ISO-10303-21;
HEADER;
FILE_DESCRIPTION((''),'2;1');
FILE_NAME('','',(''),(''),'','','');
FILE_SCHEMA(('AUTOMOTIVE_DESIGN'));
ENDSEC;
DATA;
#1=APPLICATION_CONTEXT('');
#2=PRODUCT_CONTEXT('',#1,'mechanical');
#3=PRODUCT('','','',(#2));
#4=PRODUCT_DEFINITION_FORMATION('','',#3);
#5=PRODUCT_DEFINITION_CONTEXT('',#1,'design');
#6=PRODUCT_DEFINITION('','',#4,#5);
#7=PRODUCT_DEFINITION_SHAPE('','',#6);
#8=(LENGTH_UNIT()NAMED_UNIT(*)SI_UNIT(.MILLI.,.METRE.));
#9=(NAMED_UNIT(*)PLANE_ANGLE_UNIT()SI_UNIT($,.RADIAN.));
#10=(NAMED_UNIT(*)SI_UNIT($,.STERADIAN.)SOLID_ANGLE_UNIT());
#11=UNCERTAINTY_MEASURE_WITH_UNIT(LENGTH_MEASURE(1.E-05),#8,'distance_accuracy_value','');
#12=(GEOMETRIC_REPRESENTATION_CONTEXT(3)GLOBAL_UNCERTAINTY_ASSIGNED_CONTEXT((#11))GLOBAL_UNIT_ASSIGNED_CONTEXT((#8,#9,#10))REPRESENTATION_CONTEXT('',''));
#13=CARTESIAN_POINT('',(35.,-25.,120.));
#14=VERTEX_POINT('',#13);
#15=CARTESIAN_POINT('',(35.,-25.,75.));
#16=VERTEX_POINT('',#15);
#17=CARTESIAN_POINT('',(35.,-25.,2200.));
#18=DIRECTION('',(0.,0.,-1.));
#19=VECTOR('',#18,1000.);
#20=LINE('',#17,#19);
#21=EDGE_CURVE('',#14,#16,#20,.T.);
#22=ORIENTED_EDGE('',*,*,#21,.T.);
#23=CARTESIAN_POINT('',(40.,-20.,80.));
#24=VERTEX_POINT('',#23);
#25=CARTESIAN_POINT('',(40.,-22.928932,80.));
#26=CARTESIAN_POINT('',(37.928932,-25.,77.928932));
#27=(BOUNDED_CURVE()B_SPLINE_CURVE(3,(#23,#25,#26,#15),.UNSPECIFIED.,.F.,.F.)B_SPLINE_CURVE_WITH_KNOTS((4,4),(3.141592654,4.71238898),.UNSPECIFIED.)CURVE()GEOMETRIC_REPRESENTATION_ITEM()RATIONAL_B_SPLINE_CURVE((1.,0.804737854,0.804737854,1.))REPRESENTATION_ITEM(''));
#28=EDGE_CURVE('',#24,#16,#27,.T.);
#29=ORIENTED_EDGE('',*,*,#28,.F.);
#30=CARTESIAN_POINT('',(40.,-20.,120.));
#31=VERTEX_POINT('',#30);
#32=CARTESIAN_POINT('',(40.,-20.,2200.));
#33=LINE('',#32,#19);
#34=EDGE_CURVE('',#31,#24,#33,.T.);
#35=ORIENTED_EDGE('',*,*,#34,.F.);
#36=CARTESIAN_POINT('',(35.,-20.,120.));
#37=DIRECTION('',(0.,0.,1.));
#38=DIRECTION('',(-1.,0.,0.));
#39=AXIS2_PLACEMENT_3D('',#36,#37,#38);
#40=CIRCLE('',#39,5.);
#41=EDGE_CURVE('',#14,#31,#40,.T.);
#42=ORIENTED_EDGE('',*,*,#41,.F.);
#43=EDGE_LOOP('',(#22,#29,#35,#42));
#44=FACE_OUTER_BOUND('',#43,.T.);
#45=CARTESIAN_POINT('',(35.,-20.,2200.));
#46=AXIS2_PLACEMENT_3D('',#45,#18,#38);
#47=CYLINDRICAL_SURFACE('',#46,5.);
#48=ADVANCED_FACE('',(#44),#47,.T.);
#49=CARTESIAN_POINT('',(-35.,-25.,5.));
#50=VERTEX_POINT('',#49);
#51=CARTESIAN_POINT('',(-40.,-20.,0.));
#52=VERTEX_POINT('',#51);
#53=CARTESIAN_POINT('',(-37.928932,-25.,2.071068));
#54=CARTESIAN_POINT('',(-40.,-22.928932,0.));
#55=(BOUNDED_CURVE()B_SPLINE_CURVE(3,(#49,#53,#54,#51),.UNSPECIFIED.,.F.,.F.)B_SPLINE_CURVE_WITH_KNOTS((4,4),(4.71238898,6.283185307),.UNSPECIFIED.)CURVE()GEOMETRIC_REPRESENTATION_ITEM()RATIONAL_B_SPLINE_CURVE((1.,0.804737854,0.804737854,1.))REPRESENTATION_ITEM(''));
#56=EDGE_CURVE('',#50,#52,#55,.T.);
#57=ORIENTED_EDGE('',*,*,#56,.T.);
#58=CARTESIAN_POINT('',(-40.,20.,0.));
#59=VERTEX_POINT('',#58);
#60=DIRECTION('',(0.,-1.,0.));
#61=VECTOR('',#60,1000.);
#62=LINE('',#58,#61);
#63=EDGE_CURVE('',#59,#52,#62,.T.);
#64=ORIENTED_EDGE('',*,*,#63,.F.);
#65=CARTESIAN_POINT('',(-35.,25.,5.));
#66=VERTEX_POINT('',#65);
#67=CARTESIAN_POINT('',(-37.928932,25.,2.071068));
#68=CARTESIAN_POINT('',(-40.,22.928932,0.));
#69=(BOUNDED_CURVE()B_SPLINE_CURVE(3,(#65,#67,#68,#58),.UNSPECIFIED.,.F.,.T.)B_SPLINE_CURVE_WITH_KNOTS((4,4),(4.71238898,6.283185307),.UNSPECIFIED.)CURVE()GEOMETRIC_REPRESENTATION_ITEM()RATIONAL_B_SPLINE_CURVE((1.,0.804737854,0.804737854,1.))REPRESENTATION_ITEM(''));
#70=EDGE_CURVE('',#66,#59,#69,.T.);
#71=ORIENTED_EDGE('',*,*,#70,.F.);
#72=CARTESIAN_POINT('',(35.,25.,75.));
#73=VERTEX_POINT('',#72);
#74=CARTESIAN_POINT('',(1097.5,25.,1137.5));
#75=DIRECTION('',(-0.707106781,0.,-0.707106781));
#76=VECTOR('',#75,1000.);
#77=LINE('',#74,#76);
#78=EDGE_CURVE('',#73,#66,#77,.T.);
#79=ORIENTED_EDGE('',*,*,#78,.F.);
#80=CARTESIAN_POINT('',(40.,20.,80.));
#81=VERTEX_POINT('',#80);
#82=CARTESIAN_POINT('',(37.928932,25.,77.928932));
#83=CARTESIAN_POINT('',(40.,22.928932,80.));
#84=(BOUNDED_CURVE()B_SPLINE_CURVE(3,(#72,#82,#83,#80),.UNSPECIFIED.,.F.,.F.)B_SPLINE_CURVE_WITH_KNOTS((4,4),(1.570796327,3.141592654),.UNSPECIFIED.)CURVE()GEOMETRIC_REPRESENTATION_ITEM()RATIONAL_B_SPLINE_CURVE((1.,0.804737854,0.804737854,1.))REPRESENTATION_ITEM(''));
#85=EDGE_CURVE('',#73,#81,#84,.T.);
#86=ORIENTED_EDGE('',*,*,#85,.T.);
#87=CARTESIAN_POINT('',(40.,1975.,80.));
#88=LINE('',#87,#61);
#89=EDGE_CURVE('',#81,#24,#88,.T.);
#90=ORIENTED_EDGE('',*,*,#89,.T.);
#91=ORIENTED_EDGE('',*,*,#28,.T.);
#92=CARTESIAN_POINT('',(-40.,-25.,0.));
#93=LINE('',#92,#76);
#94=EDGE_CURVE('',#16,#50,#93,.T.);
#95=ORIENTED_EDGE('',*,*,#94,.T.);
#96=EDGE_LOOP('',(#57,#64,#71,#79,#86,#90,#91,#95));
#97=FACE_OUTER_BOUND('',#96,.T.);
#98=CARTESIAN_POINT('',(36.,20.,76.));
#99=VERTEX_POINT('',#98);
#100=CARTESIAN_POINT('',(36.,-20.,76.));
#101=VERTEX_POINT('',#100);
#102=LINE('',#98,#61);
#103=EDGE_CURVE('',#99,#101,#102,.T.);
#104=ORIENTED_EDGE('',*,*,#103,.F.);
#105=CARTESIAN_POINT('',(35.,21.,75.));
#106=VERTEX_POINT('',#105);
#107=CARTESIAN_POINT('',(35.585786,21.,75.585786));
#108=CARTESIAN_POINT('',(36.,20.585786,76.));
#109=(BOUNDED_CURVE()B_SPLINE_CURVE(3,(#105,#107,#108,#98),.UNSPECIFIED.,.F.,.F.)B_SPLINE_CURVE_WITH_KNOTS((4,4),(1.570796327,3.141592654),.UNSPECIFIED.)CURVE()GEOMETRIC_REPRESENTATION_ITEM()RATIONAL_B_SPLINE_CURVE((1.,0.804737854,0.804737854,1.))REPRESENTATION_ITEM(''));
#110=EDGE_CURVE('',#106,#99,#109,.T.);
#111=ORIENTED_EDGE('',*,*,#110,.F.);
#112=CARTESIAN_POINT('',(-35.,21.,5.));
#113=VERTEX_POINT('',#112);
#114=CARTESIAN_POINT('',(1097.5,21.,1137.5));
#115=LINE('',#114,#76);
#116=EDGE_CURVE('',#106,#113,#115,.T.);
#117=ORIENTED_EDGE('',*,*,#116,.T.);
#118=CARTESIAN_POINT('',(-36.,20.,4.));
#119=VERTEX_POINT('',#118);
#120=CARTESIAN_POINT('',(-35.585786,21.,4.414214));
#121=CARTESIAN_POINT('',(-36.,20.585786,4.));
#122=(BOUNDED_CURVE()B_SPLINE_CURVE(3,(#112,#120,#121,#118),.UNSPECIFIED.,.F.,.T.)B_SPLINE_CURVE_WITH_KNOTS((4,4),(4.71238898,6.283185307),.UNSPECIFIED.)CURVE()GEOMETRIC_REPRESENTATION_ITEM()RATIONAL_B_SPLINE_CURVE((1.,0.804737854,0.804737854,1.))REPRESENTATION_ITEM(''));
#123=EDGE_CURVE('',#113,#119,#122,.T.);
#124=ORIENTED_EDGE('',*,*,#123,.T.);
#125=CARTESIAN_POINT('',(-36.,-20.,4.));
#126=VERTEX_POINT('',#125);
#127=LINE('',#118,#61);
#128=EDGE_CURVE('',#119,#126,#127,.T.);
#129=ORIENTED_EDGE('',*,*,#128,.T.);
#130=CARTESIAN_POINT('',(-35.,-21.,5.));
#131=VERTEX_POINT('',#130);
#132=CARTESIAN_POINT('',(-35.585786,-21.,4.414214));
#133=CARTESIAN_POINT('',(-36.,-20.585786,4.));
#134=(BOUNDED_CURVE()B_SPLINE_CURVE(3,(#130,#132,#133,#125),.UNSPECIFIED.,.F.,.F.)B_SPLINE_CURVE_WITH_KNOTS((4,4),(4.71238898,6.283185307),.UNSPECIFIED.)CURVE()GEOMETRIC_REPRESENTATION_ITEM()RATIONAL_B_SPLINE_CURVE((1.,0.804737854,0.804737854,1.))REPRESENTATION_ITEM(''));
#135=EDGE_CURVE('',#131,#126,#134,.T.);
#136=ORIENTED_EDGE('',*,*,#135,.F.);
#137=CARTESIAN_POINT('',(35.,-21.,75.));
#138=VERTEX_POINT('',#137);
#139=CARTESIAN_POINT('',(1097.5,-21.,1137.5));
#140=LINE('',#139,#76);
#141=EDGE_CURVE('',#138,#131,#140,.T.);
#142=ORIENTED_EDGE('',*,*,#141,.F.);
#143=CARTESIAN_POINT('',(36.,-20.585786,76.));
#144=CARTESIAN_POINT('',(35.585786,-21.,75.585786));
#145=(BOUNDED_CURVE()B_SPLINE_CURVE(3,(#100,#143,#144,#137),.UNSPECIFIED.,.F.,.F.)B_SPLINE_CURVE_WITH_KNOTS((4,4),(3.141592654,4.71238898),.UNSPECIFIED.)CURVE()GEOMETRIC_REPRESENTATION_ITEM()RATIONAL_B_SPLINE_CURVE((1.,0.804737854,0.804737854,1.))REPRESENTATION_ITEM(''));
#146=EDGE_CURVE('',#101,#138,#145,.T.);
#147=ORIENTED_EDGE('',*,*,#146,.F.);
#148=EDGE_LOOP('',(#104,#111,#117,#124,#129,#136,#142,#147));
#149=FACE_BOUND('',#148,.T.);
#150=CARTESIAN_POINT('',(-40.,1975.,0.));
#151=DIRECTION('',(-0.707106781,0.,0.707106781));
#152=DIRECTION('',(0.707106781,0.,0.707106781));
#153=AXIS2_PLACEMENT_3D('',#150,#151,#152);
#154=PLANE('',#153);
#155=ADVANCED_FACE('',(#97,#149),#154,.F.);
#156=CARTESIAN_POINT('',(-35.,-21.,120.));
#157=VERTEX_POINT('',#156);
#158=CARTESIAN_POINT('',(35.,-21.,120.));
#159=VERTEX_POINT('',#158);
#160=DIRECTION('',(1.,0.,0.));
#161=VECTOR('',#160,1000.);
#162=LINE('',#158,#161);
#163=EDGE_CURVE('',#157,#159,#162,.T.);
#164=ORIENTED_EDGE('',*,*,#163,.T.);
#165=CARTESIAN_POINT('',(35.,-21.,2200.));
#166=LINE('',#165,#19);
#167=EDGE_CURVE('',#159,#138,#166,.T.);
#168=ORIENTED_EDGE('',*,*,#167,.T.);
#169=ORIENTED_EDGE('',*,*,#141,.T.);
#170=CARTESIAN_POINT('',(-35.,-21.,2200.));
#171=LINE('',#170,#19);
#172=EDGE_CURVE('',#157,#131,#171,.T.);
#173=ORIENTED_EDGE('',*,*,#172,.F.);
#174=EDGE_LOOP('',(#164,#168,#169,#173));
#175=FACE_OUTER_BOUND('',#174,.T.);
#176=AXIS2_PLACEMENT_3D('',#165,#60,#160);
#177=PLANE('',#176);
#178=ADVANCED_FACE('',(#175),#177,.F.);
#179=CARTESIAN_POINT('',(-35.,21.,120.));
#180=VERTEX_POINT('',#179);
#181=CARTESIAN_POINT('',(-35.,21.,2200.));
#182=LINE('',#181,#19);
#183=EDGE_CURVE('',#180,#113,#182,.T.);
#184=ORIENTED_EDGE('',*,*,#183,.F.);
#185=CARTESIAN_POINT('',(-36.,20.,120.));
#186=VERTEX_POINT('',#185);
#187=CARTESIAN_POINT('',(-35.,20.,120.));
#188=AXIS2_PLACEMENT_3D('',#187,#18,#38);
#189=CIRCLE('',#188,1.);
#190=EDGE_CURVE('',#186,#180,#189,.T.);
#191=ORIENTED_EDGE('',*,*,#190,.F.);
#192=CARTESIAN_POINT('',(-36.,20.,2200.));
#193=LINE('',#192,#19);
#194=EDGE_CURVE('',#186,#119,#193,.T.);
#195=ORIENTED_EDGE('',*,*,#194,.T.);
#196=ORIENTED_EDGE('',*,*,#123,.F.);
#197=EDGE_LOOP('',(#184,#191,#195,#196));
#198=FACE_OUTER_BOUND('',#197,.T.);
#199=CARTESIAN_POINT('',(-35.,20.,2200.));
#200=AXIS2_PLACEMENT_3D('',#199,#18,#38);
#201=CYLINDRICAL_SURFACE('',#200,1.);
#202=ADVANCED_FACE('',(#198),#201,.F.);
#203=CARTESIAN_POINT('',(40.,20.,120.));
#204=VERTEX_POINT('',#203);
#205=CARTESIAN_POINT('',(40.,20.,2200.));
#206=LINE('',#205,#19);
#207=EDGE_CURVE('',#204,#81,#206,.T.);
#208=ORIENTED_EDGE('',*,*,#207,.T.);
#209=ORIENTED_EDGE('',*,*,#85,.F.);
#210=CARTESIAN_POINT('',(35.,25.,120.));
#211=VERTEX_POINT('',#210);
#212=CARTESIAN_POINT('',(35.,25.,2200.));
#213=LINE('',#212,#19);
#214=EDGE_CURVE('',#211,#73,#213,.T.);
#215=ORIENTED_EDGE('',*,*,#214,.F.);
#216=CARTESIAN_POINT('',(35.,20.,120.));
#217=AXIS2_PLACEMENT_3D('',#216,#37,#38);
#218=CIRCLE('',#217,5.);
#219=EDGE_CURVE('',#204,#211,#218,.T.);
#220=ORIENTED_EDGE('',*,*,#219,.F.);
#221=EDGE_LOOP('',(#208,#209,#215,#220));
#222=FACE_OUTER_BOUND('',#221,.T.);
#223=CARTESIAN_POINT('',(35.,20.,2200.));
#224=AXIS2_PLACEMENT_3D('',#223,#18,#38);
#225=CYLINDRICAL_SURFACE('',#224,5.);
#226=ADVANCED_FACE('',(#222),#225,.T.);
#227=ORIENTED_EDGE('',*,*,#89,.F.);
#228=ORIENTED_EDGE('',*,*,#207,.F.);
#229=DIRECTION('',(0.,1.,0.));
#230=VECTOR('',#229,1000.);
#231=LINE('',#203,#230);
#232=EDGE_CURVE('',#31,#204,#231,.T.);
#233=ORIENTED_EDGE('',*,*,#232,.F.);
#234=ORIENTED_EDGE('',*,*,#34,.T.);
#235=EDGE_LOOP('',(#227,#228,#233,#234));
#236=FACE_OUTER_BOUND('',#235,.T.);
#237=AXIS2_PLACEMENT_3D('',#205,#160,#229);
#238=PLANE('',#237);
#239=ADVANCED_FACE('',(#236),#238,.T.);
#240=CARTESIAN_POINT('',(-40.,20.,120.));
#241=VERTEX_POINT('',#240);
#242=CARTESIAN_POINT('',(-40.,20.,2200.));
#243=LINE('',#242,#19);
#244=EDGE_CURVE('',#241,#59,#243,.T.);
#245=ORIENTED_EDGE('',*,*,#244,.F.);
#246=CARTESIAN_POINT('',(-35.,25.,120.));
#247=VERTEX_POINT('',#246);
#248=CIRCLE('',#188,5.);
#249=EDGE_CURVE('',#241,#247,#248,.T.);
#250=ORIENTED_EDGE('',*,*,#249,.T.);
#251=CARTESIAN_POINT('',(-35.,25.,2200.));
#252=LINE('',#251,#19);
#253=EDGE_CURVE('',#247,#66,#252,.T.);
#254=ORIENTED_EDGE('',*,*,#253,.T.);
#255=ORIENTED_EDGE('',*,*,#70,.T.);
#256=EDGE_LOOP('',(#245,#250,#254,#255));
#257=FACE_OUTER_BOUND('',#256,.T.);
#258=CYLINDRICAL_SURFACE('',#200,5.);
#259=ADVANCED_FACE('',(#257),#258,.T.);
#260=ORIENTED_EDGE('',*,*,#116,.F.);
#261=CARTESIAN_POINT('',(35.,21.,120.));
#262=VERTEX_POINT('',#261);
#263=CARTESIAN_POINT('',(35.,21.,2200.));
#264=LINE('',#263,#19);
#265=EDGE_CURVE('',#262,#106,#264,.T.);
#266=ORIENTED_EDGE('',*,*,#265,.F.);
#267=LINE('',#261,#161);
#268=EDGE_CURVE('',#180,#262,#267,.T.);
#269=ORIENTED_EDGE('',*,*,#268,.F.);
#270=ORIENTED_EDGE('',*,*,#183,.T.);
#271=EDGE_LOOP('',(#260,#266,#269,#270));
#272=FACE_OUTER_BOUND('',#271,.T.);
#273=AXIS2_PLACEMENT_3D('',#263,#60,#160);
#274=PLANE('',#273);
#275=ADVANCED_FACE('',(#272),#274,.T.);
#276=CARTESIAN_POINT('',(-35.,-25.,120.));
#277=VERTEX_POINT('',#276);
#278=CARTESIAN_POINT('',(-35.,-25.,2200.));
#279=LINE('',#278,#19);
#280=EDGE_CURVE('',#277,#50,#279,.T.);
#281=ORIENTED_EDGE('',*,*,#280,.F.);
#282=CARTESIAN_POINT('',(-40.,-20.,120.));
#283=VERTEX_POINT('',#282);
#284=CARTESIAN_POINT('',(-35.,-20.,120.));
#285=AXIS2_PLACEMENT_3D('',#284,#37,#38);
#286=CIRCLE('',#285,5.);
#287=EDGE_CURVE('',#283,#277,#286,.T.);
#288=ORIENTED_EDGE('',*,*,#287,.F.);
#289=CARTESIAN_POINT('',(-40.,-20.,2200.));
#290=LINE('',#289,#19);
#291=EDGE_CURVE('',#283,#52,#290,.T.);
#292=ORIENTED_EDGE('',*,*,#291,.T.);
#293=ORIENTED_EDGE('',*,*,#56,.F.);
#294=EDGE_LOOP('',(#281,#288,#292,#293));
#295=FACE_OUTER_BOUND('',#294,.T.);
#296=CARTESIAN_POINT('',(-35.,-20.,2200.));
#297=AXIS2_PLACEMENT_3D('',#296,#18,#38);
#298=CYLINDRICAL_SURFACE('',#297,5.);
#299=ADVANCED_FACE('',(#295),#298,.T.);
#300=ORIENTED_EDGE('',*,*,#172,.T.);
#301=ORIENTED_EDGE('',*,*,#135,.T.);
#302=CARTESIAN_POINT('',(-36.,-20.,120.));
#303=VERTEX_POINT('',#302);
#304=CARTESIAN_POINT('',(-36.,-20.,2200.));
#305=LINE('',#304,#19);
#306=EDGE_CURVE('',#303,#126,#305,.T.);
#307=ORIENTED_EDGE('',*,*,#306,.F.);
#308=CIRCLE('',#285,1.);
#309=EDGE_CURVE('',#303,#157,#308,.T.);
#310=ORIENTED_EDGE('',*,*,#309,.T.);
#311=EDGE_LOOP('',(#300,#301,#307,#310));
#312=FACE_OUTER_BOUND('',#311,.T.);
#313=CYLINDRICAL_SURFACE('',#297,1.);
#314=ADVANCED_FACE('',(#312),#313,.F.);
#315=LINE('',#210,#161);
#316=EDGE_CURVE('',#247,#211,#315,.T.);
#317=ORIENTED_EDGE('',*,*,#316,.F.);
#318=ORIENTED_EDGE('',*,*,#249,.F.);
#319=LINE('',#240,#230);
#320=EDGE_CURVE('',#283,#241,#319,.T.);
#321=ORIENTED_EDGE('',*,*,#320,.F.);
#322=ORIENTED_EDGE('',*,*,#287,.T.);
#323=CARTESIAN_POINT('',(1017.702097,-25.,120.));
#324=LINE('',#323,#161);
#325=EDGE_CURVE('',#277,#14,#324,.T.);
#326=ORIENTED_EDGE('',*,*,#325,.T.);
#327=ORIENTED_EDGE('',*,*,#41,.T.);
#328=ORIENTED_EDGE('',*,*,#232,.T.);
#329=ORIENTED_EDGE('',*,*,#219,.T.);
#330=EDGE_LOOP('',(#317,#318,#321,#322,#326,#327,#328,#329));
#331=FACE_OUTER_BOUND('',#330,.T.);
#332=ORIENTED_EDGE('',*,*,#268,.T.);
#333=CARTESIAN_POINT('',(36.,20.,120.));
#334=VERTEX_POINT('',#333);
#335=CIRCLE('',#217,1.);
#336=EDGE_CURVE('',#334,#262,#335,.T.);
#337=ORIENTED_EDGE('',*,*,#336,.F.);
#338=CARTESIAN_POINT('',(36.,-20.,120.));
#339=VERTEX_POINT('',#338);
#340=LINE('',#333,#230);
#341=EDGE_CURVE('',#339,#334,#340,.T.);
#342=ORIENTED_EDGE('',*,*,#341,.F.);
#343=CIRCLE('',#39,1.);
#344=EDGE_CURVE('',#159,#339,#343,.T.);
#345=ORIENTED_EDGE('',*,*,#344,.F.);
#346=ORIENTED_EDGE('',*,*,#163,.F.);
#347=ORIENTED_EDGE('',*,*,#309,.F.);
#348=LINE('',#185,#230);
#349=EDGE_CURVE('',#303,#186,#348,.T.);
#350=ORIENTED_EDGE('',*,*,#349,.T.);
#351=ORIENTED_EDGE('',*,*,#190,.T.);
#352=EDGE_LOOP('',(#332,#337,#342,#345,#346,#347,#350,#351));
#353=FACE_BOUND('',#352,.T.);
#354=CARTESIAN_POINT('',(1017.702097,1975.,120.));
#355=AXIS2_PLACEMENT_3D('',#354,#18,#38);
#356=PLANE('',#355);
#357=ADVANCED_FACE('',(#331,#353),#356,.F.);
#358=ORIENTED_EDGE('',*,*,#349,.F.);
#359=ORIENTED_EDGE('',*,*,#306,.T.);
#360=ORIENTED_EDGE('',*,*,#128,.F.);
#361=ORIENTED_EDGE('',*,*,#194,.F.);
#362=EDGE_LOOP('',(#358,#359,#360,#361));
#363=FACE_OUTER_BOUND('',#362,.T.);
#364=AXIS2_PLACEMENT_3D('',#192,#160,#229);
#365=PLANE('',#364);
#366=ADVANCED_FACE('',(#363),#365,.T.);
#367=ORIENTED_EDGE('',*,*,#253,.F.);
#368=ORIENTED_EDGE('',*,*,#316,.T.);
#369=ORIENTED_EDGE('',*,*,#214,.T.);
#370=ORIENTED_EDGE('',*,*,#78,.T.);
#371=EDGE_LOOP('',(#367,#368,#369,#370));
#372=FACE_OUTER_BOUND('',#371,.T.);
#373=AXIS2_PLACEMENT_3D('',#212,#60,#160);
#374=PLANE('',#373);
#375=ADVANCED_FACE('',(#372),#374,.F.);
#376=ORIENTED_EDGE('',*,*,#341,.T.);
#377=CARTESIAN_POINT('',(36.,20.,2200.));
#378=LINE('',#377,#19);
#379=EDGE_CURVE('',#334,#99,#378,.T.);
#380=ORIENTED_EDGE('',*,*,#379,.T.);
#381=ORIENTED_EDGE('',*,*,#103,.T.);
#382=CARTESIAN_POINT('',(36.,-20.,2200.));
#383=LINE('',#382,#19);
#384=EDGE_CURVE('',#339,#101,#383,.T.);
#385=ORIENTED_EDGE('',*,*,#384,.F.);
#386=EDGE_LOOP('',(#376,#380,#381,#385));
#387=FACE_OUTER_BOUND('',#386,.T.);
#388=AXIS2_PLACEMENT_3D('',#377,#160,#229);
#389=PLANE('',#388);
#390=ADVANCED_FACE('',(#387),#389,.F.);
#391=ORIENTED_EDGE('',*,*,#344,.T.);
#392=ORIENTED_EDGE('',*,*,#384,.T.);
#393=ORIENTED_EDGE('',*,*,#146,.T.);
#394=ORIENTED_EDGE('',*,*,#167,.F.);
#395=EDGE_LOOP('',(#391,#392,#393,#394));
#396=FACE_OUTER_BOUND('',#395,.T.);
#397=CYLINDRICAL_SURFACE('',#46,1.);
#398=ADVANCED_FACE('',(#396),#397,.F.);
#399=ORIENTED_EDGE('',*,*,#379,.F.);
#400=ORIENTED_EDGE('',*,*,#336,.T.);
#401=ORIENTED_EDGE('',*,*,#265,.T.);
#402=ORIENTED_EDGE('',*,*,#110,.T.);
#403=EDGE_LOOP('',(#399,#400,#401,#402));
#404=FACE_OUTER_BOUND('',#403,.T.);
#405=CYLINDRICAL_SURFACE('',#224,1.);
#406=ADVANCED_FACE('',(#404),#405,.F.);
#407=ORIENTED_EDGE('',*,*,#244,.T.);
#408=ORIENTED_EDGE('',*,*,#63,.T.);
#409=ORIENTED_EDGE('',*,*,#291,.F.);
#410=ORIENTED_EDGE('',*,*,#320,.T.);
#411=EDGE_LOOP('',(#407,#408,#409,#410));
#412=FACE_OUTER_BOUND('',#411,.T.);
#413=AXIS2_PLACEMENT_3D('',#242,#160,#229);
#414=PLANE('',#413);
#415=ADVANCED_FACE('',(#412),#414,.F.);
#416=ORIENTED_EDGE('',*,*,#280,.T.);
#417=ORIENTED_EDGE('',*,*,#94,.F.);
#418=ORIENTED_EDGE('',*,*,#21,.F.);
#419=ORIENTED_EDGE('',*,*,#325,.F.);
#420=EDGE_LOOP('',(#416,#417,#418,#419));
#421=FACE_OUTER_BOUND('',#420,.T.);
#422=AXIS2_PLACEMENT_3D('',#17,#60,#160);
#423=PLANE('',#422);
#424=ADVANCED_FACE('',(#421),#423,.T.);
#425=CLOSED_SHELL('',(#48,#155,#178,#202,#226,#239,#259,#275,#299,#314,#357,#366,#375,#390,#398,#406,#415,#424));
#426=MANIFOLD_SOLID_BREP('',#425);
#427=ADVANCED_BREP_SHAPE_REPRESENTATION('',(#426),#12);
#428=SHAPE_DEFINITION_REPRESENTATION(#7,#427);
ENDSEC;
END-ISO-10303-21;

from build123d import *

# Parameters (mm, degrees)
BOSS_EXTRUDE1_DEPTH = 2200
SHELL1_T            = -4
SKETCH2_R           = 3.25
CUT_EXTRUDE1_DEPTH  = 10
CUT_EXTRUDE2_DEPTH  = 2000
SKETCH4_W           = 2035.40419349
SKETCH4_H           = 2143.359963821
CUT_EXTRUDE3_DEPTH  = 2000


with BuildPart() as part:
    # Sketch1 → Boss-Extrude1 (new body)
    with BuildSketch(Plane.XY):
        with BuildLine():
            Line((35, 25), (-35, 25))
            ThreePointArc((-35, 25), (-38.535533906, 23.535533906), (-40, 20))
            Line((-40, 20), (-40, -20))
            ThreePointArc((-40, -20), (-38.535533906, -23.535533906), (-35, -25))
            Line((-35, -25), (35, -25))
            ThreePointArc((35, -25), (38.535533906, -23.535533906), (40, -20))
            Line((40, -20), (40, 20))
            ThreePointArc((40, 20), (38.535533906, 23.535533906), (35, 25))
        make_face()
    extrude(amount=BOSS_EXTRUDE1_DEPTH)

    # Shell1
    shell1_openings = [part.faces().sort_by_distance(p)[0] for p in [
        (0, 0, 2200),
        (0, 0, 0),
    ]]
    offset(amount=SHELL1_T, openings=shell1_openings, kind=Kind.INTERSECTION)

    # Sketch2 → Cut-Extrude1 (cut)
    with BuildSketch(Plane(origin=(0, 25, 0), x_dir=(1, 0, 0), z_dir=(0, 1, 0))):
        with Locations(Location((-25, -919, 0), (0, 0, 180))):
            Circle(SKETCH2_R)
        with Locations(Location((25, -919, 0), (0, 0, 180))):
            Circle(SKETCH2_R)
        with Locations(Location((-25, -849, 0), (0, 0, 180))):
            Circle(SKETCH2_R)
        with Locations(Location((25, -849, 0), (0, 0, 180))):
            Circle(SKETCH2_R)
        with Locations(Location((-25, -1281, 0), (0, 0, 180))):
            Circle(SKETCH2_R)
        with Locations(Location((25, -1281, 0), (0, 0, 180))):
            Circle(SKETCH2_R)
        with Locations(Location((-25, -1351, 0), (0, 0, 180))):
            Circle(SKETCH2_R)
        with Locations(Location((25, -1351, 0), (0, 0, 180))):
            Circle(SKETCH2_R)
    extrude(amount=-CUT_EXTRUDE1_DEPTH, mode=Mode.SUBTRACT)

    # Sketch3 → Cut-Extrude2 (cut)
    with BuildSketch(Plane.XZ.offset(25)):
        Polygon((-40, 2200), (40, 2120), (40, 2200), align=None)
        Polygon((40, 80), (40, 0), (-40, 0), align=None)
    extrude(amount=-CUT_EXTRUDE2_DEPTH, mode=Mode.SUBTRACT)

    # Sketch4 → Cut-Extrude3 (cut)
    with BuildSketch(Plane.XZ.offset(25)):
        with Locations((0, 1191.679981911)):
            Rectangle(SKETCH4_W, SKETCH4_H)
    extrude(amount=-CUT_EXTRUDE3_DEPTH, mode=Mode.SUBTRACT)


solid = part.part
